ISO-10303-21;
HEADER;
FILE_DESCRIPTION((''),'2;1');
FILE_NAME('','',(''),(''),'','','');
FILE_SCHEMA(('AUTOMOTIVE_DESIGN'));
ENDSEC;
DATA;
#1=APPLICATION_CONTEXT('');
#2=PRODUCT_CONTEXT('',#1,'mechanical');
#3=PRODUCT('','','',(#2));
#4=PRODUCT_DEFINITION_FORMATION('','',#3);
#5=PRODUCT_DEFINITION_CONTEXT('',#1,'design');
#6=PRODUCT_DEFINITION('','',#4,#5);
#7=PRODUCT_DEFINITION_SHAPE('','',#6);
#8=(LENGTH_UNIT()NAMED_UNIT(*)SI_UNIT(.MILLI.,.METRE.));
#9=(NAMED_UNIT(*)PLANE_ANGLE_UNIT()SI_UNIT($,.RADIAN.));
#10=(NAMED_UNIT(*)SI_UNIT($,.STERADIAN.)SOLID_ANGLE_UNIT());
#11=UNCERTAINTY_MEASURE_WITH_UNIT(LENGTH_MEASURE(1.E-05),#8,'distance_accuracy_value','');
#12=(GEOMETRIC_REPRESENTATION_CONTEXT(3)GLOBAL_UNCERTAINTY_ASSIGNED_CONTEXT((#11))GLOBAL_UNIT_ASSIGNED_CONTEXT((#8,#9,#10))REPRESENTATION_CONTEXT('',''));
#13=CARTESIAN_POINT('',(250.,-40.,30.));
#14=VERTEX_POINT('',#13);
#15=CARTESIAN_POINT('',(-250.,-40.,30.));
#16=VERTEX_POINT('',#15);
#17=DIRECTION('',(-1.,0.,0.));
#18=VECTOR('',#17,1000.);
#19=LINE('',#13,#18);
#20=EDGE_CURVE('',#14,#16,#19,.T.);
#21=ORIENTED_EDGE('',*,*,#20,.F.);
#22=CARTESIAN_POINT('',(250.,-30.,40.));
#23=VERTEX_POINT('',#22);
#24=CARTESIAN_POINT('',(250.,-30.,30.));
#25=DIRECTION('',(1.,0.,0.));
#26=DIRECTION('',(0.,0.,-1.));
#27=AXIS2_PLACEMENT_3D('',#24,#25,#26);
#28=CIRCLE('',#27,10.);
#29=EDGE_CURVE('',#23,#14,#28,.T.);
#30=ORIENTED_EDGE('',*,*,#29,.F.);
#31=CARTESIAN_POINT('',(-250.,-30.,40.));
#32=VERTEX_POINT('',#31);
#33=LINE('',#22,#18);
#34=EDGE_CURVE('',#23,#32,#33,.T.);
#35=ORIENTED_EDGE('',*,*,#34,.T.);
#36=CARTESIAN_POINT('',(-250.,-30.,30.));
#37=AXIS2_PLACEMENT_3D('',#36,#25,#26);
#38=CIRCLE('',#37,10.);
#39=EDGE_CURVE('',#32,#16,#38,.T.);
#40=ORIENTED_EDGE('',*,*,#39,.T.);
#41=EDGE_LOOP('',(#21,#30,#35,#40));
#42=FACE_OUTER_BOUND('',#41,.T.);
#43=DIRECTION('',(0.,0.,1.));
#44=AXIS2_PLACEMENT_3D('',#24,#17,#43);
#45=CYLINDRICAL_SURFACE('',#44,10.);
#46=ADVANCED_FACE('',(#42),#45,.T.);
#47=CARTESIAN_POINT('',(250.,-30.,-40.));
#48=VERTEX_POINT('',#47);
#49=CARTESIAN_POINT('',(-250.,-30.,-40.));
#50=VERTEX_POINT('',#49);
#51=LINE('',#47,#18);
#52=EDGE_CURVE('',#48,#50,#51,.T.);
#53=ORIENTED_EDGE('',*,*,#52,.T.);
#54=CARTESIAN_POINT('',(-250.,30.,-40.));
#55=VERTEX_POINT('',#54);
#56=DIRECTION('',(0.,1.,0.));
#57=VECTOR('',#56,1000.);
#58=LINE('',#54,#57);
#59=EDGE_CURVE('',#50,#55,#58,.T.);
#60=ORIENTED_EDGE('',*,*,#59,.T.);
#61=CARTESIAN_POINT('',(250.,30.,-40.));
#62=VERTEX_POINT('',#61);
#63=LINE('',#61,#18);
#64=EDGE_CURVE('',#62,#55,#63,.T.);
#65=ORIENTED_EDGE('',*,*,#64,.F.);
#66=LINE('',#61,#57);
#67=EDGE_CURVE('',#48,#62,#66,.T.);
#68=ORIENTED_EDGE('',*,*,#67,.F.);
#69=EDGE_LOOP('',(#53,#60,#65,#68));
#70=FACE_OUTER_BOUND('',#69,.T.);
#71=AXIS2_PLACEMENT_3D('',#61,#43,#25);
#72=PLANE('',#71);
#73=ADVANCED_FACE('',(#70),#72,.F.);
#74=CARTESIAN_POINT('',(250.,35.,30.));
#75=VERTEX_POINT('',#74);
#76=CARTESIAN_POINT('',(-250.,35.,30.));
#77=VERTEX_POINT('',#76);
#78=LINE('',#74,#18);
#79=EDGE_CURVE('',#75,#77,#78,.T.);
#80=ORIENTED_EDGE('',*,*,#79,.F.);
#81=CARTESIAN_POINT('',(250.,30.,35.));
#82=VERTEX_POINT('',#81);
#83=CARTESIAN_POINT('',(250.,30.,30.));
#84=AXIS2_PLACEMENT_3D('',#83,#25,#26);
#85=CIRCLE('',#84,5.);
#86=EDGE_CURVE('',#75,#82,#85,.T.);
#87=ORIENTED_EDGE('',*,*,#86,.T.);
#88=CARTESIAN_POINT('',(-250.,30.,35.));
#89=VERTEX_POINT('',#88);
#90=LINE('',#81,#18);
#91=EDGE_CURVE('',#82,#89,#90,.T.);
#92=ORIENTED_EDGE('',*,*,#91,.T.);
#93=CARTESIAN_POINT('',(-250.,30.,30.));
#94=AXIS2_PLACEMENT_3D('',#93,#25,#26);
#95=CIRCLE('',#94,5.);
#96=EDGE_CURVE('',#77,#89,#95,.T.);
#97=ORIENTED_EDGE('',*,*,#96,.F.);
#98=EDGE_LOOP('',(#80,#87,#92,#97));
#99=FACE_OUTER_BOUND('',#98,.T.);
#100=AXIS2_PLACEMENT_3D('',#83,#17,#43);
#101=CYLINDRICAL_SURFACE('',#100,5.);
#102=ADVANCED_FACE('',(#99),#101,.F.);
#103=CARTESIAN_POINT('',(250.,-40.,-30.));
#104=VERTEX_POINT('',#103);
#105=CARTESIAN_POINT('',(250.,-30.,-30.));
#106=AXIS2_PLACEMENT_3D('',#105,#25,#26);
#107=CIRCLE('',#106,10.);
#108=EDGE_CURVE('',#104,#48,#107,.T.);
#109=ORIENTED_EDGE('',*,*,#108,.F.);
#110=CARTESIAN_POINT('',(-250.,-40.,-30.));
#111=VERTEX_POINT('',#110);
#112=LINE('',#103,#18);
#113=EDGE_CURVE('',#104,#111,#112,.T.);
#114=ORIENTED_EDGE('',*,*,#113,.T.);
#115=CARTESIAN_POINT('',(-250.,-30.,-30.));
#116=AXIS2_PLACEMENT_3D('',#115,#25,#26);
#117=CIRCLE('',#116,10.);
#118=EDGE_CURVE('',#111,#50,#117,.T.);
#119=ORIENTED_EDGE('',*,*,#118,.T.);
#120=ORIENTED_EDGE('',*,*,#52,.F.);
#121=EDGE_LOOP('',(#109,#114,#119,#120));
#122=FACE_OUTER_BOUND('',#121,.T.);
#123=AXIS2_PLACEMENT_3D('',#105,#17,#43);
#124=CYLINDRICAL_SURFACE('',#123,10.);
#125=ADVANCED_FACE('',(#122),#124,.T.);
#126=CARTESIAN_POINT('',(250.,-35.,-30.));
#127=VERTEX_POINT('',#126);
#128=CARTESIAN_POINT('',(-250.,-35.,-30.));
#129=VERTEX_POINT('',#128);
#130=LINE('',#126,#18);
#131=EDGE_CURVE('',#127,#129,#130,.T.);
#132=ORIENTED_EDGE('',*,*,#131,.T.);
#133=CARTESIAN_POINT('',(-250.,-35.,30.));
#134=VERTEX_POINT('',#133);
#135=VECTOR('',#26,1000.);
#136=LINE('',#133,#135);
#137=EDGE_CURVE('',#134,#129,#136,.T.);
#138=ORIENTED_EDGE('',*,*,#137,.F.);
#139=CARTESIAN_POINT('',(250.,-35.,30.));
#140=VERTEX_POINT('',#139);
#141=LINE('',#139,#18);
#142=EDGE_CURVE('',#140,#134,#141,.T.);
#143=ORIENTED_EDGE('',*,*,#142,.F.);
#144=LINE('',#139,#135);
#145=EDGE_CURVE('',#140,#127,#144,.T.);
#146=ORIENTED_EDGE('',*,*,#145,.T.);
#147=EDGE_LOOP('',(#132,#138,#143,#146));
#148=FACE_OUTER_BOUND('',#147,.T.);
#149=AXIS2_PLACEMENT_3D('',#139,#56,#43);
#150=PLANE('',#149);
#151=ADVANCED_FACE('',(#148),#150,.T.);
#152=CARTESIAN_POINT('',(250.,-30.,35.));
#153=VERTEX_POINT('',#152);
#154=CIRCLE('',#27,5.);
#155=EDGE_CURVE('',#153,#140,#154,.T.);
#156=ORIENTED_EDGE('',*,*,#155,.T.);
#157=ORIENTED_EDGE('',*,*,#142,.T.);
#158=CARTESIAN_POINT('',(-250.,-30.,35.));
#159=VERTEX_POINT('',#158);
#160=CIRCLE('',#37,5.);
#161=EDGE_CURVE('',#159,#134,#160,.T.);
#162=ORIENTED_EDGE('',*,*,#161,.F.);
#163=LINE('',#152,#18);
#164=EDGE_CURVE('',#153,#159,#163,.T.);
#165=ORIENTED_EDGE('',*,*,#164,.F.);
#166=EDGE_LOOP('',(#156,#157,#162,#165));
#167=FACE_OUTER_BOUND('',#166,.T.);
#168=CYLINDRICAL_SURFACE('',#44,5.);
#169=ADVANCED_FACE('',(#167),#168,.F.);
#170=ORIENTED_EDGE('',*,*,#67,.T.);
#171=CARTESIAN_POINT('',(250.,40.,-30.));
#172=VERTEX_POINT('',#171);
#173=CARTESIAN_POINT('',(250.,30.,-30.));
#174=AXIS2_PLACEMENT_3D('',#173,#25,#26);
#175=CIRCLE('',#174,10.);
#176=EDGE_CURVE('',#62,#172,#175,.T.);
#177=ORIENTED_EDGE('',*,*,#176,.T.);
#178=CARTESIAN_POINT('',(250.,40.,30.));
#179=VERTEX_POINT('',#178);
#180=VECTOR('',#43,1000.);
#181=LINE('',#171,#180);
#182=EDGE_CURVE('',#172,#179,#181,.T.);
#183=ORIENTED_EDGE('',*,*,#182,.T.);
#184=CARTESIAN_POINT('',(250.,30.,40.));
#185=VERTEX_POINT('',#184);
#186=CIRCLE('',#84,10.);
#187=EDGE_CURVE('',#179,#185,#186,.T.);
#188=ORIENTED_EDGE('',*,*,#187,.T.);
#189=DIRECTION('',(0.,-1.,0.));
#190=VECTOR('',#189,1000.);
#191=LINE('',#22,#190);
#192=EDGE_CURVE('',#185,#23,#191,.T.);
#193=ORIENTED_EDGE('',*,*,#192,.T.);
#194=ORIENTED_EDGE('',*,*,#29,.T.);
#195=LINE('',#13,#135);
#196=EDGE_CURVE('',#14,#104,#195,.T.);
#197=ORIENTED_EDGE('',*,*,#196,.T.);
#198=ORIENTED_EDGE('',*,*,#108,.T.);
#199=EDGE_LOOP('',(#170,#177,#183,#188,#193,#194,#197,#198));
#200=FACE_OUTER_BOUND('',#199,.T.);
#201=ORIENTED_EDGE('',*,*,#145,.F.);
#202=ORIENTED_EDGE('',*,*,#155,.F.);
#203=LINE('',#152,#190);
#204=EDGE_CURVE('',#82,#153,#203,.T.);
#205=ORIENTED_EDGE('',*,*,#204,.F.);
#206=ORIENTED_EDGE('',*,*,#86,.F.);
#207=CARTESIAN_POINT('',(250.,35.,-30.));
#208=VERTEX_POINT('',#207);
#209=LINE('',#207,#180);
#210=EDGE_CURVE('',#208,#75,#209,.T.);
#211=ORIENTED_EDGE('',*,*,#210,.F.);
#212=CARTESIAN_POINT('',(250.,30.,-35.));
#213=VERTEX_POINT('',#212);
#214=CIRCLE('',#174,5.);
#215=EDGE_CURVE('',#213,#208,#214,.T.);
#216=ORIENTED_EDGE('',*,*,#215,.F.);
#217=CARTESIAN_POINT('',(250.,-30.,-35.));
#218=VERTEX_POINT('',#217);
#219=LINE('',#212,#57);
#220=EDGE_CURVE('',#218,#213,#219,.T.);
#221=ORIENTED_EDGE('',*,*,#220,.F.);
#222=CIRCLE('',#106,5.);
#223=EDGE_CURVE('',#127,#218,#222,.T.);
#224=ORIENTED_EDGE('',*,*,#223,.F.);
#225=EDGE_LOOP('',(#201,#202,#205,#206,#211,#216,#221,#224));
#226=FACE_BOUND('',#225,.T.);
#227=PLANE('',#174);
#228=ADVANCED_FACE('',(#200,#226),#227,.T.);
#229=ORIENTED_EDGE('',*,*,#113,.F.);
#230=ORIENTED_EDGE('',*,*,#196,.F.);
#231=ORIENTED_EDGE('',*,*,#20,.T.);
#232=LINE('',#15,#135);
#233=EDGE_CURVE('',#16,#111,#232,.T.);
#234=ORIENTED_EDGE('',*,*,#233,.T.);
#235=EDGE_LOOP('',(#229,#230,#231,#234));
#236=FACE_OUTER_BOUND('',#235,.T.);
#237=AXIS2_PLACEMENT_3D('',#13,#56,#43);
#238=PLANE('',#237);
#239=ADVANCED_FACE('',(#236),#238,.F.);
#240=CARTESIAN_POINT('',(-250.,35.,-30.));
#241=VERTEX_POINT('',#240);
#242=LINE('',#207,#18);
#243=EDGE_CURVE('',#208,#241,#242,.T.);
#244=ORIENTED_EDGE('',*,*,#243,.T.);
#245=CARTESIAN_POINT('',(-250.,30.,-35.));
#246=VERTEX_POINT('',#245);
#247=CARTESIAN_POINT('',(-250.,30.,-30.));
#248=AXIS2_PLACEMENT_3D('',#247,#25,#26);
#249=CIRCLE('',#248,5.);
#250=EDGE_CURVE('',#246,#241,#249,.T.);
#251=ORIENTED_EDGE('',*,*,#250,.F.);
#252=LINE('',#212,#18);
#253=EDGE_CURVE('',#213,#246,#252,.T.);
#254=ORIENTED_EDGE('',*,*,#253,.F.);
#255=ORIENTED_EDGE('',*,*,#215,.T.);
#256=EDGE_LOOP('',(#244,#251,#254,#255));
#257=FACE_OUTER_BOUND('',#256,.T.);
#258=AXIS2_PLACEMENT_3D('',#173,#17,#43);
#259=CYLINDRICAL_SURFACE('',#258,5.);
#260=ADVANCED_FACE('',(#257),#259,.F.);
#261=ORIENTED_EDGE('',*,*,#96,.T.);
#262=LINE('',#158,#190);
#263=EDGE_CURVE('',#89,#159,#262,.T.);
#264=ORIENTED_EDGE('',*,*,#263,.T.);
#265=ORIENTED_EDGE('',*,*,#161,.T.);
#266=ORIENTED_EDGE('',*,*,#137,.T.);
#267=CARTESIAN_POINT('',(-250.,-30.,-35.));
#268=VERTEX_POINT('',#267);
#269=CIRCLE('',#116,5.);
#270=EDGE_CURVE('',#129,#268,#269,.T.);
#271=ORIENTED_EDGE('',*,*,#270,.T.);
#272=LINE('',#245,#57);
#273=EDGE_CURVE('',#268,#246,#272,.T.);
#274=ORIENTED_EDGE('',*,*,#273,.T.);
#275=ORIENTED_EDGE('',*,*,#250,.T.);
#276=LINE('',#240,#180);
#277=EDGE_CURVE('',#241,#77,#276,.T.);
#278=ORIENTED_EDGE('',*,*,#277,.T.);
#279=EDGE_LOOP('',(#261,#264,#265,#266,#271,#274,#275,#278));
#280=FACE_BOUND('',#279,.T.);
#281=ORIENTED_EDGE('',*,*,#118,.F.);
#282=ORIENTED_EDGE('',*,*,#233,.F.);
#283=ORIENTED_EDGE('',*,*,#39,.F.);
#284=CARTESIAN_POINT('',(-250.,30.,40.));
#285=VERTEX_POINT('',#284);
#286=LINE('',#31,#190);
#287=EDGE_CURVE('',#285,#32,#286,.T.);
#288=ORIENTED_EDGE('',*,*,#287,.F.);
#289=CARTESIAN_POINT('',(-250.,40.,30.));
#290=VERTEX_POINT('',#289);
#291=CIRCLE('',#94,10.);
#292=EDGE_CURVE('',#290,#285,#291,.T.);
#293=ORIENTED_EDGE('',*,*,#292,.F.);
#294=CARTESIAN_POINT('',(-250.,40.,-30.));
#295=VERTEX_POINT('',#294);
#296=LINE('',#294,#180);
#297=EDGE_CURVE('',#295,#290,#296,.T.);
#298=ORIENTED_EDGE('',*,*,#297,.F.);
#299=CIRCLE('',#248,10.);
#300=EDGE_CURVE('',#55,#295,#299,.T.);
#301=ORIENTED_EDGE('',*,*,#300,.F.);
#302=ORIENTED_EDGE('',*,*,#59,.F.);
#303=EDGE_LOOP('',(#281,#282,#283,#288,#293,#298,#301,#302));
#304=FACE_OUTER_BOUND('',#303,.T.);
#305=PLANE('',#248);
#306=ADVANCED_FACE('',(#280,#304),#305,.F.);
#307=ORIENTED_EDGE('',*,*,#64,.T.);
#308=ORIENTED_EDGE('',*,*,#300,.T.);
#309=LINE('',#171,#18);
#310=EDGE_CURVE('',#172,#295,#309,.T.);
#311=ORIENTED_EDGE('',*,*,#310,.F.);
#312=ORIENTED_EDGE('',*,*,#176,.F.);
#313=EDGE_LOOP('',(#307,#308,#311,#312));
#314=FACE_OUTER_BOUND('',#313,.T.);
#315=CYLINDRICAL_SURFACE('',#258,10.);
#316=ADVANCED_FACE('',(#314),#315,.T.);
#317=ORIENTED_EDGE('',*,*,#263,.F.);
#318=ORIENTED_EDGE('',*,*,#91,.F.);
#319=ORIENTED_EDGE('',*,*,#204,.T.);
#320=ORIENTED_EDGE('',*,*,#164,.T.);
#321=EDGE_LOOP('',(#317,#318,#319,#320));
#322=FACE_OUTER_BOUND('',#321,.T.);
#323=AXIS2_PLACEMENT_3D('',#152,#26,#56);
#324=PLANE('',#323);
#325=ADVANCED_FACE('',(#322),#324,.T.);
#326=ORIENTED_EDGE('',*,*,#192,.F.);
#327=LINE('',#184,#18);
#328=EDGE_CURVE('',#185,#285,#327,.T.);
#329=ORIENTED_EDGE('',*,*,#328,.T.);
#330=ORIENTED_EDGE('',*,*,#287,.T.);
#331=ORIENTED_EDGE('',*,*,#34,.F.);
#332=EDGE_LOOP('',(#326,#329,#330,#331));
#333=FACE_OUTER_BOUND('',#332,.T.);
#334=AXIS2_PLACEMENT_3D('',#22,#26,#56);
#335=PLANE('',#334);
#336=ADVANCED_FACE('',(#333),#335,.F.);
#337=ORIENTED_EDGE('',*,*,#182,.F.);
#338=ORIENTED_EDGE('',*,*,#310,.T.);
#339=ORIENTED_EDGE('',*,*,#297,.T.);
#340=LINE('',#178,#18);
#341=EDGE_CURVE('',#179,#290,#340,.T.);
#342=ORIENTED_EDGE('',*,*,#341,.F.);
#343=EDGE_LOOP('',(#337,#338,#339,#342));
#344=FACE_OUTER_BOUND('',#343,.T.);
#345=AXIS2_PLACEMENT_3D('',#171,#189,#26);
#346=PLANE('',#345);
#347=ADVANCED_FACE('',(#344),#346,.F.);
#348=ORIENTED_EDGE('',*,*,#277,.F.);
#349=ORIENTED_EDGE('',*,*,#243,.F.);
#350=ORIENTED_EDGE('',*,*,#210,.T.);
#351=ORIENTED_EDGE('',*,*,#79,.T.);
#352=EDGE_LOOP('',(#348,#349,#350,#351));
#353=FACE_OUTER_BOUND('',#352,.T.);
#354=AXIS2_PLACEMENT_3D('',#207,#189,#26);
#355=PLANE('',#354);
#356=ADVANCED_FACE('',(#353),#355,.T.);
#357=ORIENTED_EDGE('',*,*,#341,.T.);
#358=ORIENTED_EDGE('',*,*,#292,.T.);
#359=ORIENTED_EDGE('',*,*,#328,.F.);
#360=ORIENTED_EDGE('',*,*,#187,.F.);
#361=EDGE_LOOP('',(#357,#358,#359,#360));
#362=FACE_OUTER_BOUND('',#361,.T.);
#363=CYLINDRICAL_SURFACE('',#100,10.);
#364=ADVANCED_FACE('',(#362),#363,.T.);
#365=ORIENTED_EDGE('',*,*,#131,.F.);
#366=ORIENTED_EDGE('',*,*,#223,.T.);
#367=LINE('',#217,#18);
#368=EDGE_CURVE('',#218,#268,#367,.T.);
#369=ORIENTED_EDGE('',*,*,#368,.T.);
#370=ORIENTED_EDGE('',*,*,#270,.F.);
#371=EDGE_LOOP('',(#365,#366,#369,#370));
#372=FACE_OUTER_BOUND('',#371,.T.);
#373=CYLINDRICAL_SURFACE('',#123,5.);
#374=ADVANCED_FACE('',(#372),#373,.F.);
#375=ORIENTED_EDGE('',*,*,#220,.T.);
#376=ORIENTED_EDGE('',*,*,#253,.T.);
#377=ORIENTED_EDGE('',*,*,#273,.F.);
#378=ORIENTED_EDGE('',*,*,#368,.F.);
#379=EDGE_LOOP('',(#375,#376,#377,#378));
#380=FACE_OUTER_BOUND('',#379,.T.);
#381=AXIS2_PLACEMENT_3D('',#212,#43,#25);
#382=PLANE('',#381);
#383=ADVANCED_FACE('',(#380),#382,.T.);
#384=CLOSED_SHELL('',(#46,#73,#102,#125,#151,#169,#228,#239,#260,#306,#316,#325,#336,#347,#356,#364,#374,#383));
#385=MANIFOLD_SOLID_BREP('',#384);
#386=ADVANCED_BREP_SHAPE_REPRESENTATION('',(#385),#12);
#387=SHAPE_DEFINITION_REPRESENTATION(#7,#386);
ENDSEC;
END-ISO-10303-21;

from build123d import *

# Parameters (mm, degrees)
SQUARE_TUBE_80_X_80_X_5_0_1_DEPTH = 500


with BuildPart() as part:
    # Sketch1 → Square Tube 80 X 80 X 5.0(1) (new body)
    with BuildSketch(Plane(origin=(-250, 0, 0), x_dir=(0, 0, -1), z_dir=(1, 0, 0))):
        with BuildLine():
            Line((-30, -40), (30, -40))
            ThreePointArc((30, -40), (37.071067812, -37.071067812), (40, -30))
            Line((40, -30), (40, 30))
            ThreePointArc((40, 30), (37.071067812, 37.071067812), (30, 40))
            Line((30, 40), (-30, 40))
            ThreePointArc((-30, 40), (-37.071067812, 37.071067812), (-40, 30))
            Line((-40, 30), (-40, -30))
            ThreePointArc((-40, -30), (-37.071067812, -37.071067812), (-30, -40))
        make_face()
        with BuildLine():
            Line((-30, -35), (30, -35))
            ThreePointArc((30, -35), (33.535533906, -33.535533906), (35, -30))
            Line((35, -30), (35, 30))
            ThreePointArc((35, 30), (33.535533906, 33.535533906), (30, 35))
            Line((30, 35), (-30, 35))
            ThreePointArc((-30, 35), (-33.535533906, 33.535533906), (-35, 30))
            Line((-35, 30), (-35, -30))
            ThreePointArc((-35, -30), (-33.535533906, -33.535533906), (-30, -35))
        make_face(mode=Mode.SUBTRACT)
    extrude(amount=SQUARE_TUBE_80_X_80_X_5_0_1_DEPTH)


solid = part.part
